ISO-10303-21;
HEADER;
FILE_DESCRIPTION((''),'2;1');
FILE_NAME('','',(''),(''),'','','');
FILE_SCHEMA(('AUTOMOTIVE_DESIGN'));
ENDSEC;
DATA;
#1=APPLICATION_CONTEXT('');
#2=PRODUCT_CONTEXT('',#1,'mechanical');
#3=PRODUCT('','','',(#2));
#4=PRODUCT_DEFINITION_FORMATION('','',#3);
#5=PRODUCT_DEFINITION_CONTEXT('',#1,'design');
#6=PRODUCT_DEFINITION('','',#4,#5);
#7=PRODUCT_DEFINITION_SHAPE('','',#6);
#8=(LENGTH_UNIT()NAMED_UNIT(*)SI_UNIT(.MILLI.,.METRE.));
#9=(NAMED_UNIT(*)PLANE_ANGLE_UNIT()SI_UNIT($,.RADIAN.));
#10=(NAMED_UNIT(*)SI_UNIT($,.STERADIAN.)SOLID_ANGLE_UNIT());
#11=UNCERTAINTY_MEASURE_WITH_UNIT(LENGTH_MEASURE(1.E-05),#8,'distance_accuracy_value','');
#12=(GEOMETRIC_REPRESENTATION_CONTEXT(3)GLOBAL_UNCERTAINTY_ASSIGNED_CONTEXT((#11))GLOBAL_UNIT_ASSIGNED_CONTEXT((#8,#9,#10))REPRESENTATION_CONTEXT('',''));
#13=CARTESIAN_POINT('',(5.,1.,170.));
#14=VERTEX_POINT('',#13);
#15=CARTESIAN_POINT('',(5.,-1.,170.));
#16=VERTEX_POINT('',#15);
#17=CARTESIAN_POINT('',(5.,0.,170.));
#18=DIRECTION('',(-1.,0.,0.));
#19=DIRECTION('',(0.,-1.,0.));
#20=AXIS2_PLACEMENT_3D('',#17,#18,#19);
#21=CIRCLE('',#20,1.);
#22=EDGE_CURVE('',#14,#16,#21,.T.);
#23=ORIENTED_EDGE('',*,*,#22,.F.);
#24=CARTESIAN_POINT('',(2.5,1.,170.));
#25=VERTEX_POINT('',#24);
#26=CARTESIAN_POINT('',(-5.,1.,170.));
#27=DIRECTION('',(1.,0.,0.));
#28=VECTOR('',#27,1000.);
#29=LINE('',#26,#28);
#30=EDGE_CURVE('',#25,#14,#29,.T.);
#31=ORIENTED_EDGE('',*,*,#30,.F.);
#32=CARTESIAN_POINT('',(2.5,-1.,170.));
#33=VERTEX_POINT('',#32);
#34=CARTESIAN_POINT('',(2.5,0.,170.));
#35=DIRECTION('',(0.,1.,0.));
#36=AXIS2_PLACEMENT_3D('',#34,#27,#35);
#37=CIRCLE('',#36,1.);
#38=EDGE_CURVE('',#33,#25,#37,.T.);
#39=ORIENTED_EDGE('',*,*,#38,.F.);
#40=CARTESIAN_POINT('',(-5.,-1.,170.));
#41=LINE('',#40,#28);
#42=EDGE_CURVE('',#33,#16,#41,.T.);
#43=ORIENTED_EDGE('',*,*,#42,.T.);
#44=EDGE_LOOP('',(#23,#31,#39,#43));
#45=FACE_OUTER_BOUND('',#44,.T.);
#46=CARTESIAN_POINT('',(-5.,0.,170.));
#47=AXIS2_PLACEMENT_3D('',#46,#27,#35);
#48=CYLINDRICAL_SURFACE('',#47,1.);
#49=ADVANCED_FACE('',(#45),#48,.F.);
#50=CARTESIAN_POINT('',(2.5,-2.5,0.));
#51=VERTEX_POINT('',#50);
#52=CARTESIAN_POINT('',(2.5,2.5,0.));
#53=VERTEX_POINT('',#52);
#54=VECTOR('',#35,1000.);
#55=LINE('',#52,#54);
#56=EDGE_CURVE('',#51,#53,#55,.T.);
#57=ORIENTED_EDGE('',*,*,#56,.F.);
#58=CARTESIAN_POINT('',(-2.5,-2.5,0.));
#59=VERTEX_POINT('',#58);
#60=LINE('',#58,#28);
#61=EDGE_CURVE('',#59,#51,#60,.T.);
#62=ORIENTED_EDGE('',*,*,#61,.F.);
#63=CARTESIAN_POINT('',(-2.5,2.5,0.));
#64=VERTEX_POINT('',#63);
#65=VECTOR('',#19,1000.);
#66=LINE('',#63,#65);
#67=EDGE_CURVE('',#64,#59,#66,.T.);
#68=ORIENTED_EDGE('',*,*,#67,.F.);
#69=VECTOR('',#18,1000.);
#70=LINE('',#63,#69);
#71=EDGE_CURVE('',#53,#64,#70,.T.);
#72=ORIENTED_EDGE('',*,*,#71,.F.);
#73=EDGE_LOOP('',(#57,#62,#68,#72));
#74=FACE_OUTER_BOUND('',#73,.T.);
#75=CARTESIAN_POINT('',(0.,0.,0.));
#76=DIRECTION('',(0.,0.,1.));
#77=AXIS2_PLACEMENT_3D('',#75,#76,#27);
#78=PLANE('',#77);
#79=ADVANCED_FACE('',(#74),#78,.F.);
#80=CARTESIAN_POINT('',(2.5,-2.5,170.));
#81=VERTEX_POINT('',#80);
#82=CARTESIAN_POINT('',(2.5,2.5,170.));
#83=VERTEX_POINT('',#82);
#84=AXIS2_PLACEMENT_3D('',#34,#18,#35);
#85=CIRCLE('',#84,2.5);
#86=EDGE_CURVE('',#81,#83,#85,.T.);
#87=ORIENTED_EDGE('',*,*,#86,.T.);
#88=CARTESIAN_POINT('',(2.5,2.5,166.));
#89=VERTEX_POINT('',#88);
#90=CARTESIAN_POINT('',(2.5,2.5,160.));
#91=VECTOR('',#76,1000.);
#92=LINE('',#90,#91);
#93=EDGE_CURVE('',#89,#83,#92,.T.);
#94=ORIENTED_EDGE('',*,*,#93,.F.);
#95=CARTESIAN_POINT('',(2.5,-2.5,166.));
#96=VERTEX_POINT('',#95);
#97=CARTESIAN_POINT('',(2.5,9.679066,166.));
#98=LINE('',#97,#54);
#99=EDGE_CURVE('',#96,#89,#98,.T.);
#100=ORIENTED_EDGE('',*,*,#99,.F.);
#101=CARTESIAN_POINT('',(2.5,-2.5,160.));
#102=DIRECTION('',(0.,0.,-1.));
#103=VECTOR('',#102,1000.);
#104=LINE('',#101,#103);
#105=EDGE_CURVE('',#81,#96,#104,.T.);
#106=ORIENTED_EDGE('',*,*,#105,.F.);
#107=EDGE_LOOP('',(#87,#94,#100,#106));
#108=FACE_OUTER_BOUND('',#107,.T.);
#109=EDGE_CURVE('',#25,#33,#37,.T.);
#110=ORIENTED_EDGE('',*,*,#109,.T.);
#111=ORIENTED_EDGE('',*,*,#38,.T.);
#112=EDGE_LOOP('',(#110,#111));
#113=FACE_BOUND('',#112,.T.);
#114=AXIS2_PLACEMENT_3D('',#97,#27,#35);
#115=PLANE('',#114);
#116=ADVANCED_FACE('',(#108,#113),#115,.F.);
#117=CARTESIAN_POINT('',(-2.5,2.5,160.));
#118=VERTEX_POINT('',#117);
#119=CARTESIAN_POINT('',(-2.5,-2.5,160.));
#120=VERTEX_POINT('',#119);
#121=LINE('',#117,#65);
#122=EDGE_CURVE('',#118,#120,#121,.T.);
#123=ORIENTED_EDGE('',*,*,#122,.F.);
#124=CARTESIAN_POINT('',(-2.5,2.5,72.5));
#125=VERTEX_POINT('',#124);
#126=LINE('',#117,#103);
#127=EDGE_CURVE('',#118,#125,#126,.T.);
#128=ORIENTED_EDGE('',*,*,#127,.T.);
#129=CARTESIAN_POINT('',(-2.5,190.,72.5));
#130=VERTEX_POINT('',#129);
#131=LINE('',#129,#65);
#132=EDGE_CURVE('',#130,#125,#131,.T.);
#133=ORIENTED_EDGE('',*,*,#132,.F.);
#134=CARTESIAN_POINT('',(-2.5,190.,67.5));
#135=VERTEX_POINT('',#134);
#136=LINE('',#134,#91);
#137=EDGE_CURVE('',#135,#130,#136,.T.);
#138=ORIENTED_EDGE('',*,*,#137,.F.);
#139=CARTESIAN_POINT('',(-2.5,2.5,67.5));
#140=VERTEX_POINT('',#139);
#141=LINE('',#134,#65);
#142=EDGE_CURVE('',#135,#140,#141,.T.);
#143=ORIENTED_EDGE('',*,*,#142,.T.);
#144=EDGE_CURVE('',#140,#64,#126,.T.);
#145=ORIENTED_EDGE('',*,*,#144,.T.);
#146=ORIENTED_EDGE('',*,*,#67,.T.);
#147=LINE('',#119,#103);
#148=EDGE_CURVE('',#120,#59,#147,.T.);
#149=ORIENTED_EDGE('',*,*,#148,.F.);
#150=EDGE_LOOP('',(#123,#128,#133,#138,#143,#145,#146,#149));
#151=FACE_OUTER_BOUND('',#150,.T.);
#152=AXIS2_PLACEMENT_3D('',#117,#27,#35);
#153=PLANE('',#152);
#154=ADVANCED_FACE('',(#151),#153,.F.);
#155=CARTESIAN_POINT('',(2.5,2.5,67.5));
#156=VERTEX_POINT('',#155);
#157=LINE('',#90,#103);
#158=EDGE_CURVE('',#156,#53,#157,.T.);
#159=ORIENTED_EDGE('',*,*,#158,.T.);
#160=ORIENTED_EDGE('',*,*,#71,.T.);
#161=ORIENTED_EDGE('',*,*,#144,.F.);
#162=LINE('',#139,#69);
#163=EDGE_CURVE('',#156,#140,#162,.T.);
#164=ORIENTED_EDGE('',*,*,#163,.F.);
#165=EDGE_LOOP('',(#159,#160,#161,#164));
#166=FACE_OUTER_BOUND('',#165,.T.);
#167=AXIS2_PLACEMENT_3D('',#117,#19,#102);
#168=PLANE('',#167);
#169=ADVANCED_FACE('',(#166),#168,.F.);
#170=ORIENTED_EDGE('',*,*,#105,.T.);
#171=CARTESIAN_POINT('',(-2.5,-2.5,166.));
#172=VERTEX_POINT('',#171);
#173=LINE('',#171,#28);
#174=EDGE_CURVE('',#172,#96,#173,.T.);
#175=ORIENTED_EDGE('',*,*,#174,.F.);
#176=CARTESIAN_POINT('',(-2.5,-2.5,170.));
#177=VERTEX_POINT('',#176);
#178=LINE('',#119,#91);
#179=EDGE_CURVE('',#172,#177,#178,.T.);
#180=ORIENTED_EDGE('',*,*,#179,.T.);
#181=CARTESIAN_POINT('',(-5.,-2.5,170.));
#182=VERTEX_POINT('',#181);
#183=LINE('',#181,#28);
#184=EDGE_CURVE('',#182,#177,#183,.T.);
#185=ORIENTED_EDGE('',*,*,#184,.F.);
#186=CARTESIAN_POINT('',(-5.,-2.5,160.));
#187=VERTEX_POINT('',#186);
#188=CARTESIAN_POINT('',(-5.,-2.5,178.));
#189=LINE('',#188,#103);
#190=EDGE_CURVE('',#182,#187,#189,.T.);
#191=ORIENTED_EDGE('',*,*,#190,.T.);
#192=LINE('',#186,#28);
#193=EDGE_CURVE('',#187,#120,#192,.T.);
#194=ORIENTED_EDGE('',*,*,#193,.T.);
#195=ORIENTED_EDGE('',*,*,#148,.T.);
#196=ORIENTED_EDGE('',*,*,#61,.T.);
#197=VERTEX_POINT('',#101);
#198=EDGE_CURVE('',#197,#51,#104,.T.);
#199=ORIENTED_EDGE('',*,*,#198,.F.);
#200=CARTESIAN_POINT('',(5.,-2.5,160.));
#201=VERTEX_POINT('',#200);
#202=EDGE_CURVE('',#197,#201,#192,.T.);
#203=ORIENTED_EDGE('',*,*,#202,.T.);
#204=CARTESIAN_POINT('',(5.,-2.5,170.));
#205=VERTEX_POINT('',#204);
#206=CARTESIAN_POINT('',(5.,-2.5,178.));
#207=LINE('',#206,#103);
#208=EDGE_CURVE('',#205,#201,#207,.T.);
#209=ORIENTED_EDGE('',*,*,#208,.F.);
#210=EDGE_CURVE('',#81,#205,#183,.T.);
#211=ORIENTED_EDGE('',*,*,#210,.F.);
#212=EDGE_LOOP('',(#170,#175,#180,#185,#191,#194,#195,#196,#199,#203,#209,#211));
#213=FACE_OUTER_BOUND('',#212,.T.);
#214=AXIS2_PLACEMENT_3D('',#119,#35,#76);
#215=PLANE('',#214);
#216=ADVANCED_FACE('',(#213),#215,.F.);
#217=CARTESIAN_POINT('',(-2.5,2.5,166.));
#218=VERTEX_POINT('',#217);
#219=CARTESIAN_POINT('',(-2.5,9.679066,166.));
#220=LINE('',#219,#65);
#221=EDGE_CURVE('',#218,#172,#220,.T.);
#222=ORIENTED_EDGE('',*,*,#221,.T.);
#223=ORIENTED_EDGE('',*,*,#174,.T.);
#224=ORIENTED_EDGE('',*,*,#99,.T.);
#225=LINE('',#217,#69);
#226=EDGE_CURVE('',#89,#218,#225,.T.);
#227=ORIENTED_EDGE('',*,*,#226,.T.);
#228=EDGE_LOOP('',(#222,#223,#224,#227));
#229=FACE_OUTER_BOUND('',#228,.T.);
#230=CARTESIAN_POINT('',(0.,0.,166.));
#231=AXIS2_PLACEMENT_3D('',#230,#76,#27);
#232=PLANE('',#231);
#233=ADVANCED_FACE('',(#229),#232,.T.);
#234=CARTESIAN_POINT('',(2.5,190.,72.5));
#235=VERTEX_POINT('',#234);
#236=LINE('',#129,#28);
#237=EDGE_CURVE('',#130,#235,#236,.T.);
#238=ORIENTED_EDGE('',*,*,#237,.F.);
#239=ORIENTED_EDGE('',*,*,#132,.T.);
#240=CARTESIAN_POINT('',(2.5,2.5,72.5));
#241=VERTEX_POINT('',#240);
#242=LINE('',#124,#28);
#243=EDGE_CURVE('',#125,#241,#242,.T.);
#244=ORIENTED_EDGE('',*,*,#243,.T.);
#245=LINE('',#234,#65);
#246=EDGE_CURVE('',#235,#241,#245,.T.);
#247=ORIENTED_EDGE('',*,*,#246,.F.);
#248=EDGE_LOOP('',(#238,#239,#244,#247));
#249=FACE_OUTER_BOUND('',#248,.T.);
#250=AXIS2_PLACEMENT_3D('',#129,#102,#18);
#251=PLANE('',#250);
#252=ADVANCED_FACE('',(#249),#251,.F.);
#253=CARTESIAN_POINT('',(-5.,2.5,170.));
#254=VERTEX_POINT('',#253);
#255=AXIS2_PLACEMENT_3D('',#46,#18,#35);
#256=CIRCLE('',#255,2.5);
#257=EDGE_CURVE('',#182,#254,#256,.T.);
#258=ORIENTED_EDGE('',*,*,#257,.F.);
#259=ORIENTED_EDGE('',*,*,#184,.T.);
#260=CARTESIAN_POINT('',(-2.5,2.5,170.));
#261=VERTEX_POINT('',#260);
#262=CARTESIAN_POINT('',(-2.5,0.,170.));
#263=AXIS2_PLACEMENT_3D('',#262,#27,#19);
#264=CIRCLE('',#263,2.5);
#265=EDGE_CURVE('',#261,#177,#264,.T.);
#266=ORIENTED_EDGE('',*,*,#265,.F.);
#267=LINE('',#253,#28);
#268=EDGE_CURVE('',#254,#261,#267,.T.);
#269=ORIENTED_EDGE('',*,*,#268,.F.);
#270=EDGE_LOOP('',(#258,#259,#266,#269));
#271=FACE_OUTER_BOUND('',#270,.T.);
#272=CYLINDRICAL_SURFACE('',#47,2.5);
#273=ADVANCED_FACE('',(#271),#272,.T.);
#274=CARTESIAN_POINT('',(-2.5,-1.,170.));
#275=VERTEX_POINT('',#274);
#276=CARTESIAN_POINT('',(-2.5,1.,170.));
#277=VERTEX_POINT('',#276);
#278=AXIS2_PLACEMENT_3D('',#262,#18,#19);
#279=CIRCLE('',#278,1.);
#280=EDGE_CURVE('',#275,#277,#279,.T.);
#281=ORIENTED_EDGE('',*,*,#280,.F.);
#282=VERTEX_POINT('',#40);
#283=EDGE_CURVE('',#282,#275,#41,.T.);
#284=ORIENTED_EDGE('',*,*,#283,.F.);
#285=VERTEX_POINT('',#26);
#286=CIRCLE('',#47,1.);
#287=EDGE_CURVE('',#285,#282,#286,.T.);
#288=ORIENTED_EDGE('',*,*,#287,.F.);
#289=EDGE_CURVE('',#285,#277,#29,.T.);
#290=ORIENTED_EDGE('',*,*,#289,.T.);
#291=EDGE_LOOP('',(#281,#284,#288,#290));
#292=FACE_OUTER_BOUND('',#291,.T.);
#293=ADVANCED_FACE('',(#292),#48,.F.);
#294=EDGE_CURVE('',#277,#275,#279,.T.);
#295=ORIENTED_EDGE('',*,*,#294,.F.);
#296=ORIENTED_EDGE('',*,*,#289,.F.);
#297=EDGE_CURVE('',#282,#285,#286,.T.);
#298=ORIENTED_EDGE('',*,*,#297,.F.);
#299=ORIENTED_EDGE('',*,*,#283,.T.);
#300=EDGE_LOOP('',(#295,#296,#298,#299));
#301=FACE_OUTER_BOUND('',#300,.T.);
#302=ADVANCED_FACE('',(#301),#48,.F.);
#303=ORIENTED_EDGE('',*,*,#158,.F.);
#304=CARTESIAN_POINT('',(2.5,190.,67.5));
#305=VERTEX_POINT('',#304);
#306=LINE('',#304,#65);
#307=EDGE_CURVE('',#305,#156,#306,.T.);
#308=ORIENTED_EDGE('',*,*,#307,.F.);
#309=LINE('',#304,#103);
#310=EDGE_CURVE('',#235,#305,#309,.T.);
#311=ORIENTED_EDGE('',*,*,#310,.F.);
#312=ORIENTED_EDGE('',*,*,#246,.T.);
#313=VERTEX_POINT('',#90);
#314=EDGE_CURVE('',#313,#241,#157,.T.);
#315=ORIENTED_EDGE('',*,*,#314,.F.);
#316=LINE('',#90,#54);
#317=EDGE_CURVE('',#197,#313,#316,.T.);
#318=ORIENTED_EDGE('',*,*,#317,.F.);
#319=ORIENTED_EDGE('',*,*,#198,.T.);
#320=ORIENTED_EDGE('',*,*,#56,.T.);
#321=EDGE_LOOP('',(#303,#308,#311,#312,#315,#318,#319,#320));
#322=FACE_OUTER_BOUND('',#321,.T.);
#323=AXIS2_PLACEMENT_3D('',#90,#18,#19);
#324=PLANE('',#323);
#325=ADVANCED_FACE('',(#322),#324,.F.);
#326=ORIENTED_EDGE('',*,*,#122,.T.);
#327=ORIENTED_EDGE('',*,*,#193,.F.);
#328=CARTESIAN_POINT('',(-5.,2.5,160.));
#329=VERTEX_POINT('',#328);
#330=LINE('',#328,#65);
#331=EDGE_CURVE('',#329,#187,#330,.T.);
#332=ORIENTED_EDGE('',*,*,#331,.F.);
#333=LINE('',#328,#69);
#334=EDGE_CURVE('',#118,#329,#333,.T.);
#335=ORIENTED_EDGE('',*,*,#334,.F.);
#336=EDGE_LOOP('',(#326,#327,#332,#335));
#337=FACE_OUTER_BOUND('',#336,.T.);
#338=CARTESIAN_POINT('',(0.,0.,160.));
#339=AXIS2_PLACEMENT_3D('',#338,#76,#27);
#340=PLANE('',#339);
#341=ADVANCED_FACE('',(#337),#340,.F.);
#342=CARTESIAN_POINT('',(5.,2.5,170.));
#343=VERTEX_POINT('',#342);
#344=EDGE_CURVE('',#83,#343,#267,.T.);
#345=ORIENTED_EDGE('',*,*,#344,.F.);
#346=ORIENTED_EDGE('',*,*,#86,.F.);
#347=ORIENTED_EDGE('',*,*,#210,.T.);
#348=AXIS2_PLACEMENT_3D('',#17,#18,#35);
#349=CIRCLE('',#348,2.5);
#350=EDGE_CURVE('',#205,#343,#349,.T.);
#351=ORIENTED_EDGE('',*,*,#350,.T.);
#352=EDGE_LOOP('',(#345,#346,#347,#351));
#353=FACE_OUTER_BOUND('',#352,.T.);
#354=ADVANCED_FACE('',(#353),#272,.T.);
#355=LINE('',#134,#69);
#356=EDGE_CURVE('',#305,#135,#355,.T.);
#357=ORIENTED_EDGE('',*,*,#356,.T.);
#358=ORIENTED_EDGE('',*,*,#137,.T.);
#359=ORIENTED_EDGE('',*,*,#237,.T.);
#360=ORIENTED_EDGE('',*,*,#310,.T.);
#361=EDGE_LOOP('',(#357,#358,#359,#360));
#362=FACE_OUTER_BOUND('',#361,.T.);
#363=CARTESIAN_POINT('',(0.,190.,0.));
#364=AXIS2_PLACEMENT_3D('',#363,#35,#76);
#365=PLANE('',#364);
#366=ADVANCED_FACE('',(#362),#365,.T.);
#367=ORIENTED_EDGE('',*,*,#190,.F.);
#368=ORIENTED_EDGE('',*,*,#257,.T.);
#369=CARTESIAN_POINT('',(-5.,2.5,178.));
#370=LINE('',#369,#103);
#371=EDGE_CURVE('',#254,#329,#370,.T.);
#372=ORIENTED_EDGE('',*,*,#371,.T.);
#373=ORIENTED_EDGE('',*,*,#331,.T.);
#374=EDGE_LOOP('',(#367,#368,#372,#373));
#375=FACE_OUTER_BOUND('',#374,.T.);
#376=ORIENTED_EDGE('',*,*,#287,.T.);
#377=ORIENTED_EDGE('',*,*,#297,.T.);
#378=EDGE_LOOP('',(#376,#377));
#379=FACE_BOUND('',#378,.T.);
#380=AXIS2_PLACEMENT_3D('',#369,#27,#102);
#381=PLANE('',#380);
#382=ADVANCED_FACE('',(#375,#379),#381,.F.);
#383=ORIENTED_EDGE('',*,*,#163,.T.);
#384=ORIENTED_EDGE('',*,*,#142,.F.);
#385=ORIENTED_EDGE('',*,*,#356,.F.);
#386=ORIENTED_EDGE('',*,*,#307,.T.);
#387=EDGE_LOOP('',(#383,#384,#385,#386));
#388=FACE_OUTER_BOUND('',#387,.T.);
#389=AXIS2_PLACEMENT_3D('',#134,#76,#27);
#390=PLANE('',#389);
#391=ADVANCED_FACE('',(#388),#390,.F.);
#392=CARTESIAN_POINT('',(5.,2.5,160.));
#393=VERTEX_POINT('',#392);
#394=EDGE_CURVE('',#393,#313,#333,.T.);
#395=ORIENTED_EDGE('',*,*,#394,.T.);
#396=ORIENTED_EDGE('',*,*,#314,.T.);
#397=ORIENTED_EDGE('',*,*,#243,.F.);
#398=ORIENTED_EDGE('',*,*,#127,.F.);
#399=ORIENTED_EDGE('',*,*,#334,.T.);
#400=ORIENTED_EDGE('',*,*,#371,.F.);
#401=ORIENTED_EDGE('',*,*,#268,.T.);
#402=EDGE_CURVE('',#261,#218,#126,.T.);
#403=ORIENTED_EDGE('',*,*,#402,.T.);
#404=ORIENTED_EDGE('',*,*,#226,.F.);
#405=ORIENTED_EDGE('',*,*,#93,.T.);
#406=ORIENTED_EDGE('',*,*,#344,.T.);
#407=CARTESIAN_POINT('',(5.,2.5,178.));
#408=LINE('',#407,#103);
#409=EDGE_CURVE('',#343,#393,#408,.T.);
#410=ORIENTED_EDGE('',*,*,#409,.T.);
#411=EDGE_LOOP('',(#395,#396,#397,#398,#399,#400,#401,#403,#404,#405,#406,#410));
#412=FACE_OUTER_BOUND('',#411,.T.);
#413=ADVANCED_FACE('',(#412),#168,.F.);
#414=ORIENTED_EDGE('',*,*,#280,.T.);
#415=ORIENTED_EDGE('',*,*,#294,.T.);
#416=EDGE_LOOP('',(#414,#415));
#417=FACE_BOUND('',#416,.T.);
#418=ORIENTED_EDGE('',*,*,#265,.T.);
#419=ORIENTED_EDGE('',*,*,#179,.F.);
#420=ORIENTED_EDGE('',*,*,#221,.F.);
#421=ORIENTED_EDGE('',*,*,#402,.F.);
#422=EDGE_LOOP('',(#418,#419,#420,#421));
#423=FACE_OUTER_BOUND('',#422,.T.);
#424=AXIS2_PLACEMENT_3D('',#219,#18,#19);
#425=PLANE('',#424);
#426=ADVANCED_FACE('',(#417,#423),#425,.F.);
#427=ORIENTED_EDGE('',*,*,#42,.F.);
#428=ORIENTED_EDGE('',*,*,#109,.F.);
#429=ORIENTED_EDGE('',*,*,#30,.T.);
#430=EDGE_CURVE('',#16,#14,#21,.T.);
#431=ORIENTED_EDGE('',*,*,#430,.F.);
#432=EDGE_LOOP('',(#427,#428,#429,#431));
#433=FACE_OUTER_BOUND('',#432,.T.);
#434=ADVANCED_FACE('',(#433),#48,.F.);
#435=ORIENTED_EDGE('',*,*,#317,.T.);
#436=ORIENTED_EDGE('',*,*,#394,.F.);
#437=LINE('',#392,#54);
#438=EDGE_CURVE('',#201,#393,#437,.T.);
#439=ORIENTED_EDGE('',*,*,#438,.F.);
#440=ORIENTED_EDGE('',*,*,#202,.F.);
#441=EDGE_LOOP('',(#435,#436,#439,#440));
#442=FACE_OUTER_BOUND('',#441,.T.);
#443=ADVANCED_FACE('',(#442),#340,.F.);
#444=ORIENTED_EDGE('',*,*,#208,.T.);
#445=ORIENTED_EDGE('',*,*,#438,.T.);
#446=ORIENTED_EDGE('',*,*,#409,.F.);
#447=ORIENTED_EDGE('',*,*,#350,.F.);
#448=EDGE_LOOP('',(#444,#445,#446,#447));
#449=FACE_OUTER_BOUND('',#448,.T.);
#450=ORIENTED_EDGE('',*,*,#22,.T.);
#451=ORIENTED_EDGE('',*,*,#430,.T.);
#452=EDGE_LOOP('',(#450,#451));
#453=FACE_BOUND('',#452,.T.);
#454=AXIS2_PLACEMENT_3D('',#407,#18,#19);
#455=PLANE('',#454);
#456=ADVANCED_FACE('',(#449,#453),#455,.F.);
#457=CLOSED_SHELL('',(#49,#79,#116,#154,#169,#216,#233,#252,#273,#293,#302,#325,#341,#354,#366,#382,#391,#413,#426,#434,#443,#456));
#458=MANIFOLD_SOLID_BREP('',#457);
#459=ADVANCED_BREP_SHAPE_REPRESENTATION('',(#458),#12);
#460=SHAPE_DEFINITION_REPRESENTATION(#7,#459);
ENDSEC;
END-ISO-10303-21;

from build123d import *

# Parameters (mm, degrees)
SKETCH1_W               = 5
SKETCH1_H               = 5
BOSS_EXTRUDE1_DEPTH     = 160
SKETCH2_W               = 10
SKETCH2_H               = 5
BOSS_EXTRUDE2_DEPTH     = 18
SKETCH3_W               = 5
SKETCH3_H               = 19.358131828
CUT_EXTRUDE1_DEPTH      = 12
CUT_EXTRUDE2_DEPTH      = 179.298205263
CUT_EXTRUDE2_DEPTH_BACK = 179.298205263
SKETCH4_R               = 1
SKETCH5_W               = 5
SKETCH5_H               = 5
BOSS_EXTRUDE3_DEPTH     = 190


with BuildPart() as part:
    # Sketch1 → Boss-Extrude1 (new body)
    with BuildSketch(Plane.XY):
        Rectangle(SKETCH1_W, SKETCH1_H)
    extrude(amount=BOSS_EXTRUDE1_DEPTH)

    # Sketch2 → Boss-Extrude2 (add)
    with BuildSketch(Plane.XY.offset(160)):
        Rectangle(SKETCH2_W, SKETCH2_H)
    extrude(amount=BOSS_EXTRUDE2_DEPTH)

    # Sketch3 → Cut-Extrude1 (cut)
    with BuildSketch(Plane.XY.offset(178)):
        Rectangle(SKETCH3_W, SKETCH3_H)
    extrude(amount=-CUT_EXTRUDE1_DEPTH, mode=Mode.SUBTRACT)

    # Sketch4 → Cut-Extrude2 (cut, two sides: drawn at the far end of the back side and taken through both)
    with BuildSketch(Plane(origin=(5, 0, 0), x_dir=(0, 0, -1), z_dir=(1, 0, 0)).offset(-CUT_EXTRUDE2_DEPTH_BACK)):
        with Locations(Location((-170, 0, 0), (0, 0, 90))):
            Circle(SKETCH4_R)
        with BuildLine():
            Line((-170, 2.5), (-170, 12.575428257))
            Line((-170, 12.575428257), (-197.273990227, 12.575428257))
            Line((-197.273990227, 12.575428257), (-202.218051786, -13.998902623))
            Line((-202.218051786, -13.998902623), (-170, -2.5))
            ThreePointArc((-170, -2.5), (-172.5, 0), (-170, 2.5))
        make_face()
    extrude(amount=CUT_EXTRUDE2_DEPTH + CUT_EXTRUDE2_DEPTH_BACK, mode=Mode.SUBTRACT)

    # Sketch5 → Boss-Extrude3 (add)
    with BuildSketch(Plane(origin=(0, 0, 0), x_dir=(1, 0, 0), z_dir=(0, 1, 0))):
        with Locations((0, -70)):
            Rectangle(SKETCH5_W, SKETCH5_H)
    extrude(amount=BOSS_EXTRUDE3_DEPTH)


solid = part.part
